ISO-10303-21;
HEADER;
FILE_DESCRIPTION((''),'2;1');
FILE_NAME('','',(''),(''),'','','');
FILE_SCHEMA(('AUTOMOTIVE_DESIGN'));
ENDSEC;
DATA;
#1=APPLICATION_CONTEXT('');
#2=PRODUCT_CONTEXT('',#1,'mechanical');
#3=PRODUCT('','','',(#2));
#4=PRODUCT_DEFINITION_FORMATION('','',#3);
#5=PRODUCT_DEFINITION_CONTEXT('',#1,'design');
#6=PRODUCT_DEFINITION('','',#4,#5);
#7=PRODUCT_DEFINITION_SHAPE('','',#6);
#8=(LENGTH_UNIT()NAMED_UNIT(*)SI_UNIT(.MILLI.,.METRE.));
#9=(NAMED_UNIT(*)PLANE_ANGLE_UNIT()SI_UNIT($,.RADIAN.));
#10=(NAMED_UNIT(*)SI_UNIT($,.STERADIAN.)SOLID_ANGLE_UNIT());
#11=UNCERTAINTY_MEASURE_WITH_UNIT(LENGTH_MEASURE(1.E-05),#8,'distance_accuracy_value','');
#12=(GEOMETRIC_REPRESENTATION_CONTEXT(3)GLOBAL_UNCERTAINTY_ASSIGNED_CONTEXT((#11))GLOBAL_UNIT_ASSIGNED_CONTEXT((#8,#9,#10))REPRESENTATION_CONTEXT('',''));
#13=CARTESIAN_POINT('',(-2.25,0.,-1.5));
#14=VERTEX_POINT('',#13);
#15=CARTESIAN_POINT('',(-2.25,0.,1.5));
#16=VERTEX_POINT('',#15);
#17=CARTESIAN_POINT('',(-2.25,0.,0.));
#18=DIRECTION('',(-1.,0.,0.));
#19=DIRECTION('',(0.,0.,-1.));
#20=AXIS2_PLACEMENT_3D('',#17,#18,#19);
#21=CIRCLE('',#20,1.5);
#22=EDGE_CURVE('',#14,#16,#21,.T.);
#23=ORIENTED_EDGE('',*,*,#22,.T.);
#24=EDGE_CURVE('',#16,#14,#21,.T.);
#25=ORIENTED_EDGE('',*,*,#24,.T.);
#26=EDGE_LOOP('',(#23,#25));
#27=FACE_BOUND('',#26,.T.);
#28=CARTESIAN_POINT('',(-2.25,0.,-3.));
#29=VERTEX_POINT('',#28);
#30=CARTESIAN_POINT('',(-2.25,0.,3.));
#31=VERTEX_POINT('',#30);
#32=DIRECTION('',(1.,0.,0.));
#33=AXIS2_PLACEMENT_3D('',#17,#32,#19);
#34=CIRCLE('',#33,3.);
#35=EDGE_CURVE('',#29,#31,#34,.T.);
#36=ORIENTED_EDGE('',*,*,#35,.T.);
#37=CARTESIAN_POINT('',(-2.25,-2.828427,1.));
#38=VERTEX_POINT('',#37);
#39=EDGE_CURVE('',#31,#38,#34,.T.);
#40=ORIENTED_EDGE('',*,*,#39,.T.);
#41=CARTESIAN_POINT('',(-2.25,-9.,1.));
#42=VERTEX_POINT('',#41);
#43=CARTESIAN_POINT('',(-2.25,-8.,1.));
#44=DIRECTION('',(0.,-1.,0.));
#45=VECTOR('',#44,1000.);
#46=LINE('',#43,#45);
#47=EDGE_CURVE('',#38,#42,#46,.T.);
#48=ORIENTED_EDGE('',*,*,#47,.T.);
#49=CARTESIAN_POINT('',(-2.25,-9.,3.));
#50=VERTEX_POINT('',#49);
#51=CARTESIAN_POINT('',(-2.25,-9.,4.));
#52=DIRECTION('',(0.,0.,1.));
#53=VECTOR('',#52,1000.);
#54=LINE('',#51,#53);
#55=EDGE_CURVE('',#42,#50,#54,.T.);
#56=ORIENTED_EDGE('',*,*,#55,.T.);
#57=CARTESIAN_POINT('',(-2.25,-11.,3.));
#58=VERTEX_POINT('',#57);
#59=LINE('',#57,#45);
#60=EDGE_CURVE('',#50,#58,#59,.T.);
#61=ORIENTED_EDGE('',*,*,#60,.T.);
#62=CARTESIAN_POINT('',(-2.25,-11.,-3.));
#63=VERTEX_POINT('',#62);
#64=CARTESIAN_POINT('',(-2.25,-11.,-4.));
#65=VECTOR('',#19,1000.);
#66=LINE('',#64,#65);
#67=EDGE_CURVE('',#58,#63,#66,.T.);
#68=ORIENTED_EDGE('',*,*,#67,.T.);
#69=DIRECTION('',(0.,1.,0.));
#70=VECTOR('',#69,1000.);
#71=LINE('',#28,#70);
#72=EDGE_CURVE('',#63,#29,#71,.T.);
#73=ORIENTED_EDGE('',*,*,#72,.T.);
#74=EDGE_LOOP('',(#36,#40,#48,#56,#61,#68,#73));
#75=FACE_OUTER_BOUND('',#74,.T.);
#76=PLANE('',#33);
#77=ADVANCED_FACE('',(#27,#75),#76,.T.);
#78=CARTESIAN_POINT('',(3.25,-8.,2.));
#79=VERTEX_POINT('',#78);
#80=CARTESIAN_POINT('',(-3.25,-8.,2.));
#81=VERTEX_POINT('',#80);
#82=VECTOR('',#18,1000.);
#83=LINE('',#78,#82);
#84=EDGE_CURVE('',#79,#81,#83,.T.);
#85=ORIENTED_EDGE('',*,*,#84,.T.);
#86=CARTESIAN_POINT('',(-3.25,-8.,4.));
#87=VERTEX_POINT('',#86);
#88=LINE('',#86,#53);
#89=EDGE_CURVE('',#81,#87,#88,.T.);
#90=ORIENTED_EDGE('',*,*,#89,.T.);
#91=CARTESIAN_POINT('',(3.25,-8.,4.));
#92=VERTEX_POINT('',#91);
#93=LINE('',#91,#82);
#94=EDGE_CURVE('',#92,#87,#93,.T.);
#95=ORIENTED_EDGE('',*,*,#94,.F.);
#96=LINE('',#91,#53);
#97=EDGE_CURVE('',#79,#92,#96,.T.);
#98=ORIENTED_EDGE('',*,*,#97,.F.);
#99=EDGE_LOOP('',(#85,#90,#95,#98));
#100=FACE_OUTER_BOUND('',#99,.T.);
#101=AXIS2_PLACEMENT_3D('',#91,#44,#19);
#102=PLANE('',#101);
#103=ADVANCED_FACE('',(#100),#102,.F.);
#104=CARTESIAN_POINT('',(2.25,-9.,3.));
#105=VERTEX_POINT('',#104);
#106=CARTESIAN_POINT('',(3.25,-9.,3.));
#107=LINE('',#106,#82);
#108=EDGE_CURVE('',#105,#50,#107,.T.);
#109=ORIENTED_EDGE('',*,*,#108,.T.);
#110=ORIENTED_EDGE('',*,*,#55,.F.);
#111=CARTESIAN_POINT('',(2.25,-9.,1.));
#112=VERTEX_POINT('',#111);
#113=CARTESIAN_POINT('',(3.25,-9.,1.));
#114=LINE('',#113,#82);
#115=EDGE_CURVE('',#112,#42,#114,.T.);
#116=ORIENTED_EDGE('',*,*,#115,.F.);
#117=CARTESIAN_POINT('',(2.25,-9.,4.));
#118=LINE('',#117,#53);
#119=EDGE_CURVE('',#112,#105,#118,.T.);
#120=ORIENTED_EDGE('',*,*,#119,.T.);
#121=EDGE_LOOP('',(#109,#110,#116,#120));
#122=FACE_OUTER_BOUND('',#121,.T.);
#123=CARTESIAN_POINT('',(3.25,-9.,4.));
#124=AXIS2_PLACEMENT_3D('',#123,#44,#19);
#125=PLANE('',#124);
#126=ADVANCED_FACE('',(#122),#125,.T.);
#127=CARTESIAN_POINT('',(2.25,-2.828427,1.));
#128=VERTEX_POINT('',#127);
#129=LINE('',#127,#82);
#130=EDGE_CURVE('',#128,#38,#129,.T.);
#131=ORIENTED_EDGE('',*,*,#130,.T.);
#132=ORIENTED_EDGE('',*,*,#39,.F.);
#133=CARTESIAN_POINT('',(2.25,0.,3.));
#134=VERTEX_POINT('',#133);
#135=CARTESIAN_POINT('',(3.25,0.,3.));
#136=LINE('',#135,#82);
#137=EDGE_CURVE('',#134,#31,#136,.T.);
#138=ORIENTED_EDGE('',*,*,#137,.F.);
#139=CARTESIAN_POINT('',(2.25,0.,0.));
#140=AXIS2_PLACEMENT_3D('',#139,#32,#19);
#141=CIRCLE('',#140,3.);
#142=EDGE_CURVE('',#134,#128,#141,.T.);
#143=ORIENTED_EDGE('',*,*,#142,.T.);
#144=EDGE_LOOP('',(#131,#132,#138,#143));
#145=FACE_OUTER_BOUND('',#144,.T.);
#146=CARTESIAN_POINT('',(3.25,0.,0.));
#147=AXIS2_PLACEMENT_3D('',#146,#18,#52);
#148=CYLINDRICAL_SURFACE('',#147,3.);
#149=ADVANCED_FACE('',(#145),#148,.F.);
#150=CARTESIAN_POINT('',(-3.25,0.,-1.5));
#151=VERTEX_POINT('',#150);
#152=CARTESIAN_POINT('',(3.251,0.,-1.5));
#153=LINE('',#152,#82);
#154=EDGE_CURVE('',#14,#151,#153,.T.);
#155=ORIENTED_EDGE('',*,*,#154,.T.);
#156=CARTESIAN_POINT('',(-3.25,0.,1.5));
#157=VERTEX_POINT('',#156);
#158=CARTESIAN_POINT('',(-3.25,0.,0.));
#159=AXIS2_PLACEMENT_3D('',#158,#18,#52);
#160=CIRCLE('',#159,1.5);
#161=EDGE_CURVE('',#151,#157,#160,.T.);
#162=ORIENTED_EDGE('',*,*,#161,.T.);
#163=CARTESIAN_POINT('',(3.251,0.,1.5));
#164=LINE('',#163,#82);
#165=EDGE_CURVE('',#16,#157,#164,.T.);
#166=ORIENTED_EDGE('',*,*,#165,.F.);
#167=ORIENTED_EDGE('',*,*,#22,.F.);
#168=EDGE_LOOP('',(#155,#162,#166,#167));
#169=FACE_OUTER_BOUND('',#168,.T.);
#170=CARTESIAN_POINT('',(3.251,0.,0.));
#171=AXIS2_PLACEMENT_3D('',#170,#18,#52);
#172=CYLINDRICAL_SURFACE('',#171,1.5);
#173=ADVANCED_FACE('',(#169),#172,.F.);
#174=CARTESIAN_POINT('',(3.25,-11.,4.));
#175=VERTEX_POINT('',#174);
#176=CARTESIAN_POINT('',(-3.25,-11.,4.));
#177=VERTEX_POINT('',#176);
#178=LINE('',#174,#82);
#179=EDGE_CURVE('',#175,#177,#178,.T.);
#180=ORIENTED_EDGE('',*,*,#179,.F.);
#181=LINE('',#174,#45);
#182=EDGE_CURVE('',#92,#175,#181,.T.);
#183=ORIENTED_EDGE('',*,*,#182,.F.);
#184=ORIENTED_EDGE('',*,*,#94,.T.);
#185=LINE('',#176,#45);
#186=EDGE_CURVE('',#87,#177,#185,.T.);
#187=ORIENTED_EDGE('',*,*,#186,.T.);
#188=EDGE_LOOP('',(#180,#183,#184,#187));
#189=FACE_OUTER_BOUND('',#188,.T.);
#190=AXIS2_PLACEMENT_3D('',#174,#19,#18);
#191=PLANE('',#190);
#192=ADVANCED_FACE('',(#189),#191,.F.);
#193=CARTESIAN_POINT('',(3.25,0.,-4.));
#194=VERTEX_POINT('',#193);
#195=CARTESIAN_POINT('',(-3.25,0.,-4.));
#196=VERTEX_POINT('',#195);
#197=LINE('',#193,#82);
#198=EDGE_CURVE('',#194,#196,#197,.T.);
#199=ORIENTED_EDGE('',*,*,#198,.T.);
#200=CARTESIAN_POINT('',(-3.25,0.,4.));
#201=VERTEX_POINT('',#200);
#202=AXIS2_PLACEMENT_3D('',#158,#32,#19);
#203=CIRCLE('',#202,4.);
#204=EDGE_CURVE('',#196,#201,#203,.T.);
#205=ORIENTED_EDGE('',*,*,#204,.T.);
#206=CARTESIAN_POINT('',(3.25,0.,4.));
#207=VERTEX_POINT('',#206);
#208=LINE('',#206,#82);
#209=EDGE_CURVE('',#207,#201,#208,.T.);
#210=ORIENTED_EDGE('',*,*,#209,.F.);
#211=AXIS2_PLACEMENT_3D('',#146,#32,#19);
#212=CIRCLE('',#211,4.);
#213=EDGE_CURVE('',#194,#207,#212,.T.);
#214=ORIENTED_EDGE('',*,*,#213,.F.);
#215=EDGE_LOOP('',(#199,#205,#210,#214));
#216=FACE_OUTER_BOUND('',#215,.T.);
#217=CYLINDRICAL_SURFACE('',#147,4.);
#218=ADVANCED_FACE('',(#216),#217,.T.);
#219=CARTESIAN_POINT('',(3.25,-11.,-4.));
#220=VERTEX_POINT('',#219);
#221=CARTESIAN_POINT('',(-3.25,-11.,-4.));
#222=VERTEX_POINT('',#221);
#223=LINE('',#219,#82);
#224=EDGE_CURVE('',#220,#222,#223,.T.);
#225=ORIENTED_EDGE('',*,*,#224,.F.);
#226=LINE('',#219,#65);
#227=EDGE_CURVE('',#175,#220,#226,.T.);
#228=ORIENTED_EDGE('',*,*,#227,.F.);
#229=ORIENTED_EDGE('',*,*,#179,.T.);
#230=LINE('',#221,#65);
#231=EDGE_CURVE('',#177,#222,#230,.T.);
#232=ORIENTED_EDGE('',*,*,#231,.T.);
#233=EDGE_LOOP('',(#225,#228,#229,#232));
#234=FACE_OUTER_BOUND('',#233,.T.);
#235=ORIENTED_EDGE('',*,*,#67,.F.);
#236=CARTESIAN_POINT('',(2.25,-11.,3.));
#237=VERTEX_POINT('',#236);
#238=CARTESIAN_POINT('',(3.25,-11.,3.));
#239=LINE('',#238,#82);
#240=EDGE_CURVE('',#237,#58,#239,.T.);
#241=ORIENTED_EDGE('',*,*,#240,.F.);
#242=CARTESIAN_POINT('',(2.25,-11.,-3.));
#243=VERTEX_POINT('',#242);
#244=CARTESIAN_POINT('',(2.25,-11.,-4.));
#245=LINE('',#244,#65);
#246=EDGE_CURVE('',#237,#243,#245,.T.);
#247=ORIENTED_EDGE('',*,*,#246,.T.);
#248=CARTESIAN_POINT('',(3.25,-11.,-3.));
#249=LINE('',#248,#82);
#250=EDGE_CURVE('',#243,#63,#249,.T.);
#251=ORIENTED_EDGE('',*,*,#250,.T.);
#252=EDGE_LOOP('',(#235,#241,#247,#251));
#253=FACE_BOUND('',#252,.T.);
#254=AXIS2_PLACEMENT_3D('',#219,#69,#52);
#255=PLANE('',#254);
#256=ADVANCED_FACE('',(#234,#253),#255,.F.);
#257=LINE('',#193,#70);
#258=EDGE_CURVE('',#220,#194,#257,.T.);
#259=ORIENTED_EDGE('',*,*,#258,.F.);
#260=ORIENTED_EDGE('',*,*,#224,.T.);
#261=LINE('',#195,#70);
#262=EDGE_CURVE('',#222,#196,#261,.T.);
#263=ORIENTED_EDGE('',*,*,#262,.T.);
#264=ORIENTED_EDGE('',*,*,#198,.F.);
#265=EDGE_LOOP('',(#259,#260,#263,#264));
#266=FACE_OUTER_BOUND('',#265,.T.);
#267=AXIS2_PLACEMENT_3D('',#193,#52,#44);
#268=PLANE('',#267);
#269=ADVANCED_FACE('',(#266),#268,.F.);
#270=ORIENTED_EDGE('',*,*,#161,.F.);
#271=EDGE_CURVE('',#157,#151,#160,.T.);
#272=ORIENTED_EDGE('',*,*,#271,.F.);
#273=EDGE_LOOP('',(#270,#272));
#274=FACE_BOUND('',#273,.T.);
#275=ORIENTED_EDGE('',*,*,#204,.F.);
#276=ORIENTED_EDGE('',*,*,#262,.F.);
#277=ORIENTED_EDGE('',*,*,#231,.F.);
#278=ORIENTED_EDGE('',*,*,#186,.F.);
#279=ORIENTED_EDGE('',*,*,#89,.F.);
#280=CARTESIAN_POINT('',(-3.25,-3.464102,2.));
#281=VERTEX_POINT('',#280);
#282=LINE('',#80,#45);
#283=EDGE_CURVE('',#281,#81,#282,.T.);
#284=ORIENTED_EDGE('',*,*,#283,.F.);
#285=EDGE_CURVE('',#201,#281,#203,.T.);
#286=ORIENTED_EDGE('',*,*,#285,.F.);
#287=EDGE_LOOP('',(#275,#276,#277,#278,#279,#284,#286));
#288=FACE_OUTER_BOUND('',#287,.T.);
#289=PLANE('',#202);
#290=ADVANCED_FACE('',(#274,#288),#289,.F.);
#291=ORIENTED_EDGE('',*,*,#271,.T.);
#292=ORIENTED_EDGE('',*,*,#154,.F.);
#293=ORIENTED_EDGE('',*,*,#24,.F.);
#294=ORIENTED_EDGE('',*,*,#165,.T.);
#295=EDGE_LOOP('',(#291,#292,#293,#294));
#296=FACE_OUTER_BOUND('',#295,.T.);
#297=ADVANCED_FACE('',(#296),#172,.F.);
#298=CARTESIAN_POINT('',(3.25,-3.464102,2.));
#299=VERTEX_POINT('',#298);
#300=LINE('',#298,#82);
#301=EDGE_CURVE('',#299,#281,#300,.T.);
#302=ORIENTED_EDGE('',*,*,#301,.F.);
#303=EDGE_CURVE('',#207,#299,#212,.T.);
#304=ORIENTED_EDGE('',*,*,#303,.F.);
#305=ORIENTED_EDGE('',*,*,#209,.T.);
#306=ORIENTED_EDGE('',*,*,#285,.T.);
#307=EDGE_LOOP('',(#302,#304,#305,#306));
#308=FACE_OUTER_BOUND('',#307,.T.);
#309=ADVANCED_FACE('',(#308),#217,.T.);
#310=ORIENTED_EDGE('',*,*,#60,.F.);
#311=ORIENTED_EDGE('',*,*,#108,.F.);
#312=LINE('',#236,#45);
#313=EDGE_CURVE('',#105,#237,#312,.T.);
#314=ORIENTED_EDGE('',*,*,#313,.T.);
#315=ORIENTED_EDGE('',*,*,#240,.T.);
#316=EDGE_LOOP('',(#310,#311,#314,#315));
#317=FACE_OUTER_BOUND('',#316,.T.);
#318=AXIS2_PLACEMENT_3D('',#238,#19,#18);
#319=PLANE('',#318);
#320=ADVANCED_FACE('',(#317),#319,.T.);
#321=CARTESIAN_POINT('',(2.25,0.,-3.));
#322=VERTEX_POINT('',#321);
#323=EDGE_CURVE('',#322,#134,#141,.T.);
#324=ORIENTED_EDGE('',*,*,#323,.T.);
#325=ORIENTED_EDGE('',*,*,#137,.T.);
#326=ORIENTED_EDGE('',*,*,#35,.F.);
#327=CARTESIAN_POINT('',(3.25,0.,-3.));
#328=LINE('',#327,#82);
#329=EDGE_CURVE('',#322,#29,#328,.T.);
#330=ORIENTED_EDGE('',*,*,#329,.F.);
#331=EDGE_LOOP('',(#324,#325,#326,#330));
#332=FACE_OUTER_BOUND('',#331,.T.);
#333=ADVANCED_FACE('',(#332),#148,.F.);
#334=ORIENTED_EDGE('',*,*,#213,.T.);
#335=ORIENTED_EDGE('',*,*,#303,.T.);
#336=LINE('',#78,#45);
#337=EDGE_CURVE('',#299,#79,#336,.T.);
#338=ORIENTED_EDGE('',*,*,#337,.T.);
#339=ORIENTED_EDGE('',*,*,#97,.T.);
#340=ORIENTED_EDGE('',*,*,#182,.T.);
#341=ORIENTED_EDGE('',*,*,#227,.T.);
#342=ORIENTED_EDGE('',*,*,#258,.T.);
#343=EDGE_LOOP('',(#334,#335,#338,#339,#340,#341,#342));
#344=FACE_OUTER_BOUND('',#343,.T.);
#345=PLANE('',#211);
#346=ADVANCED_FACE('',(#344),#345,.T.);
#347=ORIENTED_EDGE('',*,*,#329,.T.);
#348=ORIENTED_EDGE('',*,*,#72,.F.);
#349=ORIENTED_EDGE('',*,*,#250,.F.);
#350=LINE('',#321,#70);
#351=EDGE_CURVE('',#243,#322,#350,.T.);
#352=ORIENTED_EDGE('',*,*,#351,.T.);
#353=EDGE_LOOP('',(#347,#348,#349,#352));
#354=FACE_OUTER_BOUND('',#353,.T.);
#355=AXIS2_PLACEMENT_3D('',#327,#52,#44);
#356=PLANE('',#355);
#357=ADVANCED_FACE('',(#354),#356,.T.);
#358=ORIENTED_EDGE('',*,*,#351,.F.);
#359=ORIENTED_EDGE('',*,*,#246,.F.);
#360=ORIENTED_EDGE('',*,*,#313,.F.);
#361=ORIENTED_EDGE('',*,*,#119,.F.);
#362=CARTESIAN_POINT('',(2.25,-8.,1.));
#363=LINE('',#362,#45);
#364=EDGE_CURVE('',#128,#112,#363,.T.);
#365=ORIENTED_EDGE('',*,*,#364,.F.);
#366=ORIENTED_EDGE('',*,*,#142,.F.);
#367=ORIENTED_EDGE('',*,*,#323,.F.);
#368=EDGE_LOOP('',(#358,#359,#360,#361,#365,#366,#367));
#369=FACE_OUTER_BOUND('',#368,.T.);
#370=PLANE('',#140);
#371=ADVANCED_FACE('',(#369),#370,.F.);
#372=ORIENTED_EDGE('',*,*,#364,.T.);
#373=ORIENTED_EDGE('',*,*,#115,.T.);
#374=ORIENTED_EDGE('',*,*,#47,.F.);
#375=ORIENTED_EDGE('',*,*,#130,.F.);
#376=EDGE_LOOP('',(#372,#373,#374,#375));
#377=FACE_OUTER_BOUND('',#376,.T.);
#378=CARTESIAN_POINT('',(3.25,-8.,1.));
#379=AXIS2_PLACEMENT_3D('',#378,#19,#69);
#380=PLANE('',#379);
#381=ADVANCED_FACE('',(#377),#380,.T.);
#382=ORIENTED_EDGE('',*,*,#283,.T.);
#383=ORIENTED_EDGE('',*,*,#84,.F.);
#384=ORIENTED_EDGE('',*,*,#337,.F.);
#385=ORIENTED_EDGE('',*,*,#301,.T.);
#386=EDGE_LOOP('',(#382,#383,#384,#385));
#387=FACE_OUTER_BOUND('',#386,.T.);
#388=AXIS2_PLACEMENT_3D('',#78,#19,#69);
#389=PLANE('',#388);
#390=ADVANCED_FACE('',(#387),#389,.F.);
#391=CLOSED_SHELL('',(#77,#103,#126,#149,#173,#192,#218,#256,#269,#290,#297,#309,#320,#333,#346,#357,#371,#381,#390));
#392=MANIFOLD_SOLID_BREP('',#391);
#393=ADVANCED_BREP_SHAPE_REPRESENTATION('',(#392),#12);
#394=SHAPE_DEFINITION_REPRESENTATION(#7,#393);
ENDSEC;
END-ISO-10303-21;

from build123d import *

# Parameters (mm, degrees)
LEG_BODY_DEPTH        = 3.25
LEG_SHELL_1MM_T       = -1
HIP_PIN_HOLE_3_REACH  = 15.388
HIP_PIN_HOLE_SKETCH_R = 1.5


with BuildPart() as part:
    # Leg Profile Sketch → Leg Body (new, symmetric)
    with BuildSketch(Plane(origin=(0, 0, 0), x_dir=(0, 0, -1), z_dir=(1, 0, 0))):
        with BuildLine():
            Line((4, 0), (4, -11))
            Line((4, -11), (-4, -11))
            Line((-4, -11), (-4, -8))
            Line((-4, -8), (-2, -8))
            Line((-2, -8), (-2, -3.464101615))
            ThreePointArc((-2, -3.464101615), (-2, 3.464101615), (4, 0))
        make_face()
    extrude(amount=LEG_BODY_DEPTH, both=True)

    # Leg Shell 1mm
    leg_shell_1mm_openings = [part.faces().sort_by_distance(p)[0] for p in [
        (0, -11, 0),
    ]]
    offset(amount=LEG_SHELL_1MM_T, openings=leg_shell_1mm_openings, kind=Kind.INTERSECTION)

    # Hip Pin Hole Sketch → Hip Pin Hole Ø3 (cut, up to next)
    with BuildSketch(Plane.ZY.offset(3.25), mode=Mode.PRIVATE) as hip_pin_hole_3_sk1:
        Circle(HIP_PIN_HOLE_SKETCH_R)
    hip_pin_hole_3_tool1 = extrude(hip_pin_hole_3_sk1.sketch, amount=-HIP_PIN_HOLE_3_REACH, mode=Mode.PRIVATE) & part.part
    add(hip_pin_hole_3_tool1.solids().sort_by_distance((-3.25, 0, 0))[0], mode=Mode.SUBTRACT)


solid = part.part
